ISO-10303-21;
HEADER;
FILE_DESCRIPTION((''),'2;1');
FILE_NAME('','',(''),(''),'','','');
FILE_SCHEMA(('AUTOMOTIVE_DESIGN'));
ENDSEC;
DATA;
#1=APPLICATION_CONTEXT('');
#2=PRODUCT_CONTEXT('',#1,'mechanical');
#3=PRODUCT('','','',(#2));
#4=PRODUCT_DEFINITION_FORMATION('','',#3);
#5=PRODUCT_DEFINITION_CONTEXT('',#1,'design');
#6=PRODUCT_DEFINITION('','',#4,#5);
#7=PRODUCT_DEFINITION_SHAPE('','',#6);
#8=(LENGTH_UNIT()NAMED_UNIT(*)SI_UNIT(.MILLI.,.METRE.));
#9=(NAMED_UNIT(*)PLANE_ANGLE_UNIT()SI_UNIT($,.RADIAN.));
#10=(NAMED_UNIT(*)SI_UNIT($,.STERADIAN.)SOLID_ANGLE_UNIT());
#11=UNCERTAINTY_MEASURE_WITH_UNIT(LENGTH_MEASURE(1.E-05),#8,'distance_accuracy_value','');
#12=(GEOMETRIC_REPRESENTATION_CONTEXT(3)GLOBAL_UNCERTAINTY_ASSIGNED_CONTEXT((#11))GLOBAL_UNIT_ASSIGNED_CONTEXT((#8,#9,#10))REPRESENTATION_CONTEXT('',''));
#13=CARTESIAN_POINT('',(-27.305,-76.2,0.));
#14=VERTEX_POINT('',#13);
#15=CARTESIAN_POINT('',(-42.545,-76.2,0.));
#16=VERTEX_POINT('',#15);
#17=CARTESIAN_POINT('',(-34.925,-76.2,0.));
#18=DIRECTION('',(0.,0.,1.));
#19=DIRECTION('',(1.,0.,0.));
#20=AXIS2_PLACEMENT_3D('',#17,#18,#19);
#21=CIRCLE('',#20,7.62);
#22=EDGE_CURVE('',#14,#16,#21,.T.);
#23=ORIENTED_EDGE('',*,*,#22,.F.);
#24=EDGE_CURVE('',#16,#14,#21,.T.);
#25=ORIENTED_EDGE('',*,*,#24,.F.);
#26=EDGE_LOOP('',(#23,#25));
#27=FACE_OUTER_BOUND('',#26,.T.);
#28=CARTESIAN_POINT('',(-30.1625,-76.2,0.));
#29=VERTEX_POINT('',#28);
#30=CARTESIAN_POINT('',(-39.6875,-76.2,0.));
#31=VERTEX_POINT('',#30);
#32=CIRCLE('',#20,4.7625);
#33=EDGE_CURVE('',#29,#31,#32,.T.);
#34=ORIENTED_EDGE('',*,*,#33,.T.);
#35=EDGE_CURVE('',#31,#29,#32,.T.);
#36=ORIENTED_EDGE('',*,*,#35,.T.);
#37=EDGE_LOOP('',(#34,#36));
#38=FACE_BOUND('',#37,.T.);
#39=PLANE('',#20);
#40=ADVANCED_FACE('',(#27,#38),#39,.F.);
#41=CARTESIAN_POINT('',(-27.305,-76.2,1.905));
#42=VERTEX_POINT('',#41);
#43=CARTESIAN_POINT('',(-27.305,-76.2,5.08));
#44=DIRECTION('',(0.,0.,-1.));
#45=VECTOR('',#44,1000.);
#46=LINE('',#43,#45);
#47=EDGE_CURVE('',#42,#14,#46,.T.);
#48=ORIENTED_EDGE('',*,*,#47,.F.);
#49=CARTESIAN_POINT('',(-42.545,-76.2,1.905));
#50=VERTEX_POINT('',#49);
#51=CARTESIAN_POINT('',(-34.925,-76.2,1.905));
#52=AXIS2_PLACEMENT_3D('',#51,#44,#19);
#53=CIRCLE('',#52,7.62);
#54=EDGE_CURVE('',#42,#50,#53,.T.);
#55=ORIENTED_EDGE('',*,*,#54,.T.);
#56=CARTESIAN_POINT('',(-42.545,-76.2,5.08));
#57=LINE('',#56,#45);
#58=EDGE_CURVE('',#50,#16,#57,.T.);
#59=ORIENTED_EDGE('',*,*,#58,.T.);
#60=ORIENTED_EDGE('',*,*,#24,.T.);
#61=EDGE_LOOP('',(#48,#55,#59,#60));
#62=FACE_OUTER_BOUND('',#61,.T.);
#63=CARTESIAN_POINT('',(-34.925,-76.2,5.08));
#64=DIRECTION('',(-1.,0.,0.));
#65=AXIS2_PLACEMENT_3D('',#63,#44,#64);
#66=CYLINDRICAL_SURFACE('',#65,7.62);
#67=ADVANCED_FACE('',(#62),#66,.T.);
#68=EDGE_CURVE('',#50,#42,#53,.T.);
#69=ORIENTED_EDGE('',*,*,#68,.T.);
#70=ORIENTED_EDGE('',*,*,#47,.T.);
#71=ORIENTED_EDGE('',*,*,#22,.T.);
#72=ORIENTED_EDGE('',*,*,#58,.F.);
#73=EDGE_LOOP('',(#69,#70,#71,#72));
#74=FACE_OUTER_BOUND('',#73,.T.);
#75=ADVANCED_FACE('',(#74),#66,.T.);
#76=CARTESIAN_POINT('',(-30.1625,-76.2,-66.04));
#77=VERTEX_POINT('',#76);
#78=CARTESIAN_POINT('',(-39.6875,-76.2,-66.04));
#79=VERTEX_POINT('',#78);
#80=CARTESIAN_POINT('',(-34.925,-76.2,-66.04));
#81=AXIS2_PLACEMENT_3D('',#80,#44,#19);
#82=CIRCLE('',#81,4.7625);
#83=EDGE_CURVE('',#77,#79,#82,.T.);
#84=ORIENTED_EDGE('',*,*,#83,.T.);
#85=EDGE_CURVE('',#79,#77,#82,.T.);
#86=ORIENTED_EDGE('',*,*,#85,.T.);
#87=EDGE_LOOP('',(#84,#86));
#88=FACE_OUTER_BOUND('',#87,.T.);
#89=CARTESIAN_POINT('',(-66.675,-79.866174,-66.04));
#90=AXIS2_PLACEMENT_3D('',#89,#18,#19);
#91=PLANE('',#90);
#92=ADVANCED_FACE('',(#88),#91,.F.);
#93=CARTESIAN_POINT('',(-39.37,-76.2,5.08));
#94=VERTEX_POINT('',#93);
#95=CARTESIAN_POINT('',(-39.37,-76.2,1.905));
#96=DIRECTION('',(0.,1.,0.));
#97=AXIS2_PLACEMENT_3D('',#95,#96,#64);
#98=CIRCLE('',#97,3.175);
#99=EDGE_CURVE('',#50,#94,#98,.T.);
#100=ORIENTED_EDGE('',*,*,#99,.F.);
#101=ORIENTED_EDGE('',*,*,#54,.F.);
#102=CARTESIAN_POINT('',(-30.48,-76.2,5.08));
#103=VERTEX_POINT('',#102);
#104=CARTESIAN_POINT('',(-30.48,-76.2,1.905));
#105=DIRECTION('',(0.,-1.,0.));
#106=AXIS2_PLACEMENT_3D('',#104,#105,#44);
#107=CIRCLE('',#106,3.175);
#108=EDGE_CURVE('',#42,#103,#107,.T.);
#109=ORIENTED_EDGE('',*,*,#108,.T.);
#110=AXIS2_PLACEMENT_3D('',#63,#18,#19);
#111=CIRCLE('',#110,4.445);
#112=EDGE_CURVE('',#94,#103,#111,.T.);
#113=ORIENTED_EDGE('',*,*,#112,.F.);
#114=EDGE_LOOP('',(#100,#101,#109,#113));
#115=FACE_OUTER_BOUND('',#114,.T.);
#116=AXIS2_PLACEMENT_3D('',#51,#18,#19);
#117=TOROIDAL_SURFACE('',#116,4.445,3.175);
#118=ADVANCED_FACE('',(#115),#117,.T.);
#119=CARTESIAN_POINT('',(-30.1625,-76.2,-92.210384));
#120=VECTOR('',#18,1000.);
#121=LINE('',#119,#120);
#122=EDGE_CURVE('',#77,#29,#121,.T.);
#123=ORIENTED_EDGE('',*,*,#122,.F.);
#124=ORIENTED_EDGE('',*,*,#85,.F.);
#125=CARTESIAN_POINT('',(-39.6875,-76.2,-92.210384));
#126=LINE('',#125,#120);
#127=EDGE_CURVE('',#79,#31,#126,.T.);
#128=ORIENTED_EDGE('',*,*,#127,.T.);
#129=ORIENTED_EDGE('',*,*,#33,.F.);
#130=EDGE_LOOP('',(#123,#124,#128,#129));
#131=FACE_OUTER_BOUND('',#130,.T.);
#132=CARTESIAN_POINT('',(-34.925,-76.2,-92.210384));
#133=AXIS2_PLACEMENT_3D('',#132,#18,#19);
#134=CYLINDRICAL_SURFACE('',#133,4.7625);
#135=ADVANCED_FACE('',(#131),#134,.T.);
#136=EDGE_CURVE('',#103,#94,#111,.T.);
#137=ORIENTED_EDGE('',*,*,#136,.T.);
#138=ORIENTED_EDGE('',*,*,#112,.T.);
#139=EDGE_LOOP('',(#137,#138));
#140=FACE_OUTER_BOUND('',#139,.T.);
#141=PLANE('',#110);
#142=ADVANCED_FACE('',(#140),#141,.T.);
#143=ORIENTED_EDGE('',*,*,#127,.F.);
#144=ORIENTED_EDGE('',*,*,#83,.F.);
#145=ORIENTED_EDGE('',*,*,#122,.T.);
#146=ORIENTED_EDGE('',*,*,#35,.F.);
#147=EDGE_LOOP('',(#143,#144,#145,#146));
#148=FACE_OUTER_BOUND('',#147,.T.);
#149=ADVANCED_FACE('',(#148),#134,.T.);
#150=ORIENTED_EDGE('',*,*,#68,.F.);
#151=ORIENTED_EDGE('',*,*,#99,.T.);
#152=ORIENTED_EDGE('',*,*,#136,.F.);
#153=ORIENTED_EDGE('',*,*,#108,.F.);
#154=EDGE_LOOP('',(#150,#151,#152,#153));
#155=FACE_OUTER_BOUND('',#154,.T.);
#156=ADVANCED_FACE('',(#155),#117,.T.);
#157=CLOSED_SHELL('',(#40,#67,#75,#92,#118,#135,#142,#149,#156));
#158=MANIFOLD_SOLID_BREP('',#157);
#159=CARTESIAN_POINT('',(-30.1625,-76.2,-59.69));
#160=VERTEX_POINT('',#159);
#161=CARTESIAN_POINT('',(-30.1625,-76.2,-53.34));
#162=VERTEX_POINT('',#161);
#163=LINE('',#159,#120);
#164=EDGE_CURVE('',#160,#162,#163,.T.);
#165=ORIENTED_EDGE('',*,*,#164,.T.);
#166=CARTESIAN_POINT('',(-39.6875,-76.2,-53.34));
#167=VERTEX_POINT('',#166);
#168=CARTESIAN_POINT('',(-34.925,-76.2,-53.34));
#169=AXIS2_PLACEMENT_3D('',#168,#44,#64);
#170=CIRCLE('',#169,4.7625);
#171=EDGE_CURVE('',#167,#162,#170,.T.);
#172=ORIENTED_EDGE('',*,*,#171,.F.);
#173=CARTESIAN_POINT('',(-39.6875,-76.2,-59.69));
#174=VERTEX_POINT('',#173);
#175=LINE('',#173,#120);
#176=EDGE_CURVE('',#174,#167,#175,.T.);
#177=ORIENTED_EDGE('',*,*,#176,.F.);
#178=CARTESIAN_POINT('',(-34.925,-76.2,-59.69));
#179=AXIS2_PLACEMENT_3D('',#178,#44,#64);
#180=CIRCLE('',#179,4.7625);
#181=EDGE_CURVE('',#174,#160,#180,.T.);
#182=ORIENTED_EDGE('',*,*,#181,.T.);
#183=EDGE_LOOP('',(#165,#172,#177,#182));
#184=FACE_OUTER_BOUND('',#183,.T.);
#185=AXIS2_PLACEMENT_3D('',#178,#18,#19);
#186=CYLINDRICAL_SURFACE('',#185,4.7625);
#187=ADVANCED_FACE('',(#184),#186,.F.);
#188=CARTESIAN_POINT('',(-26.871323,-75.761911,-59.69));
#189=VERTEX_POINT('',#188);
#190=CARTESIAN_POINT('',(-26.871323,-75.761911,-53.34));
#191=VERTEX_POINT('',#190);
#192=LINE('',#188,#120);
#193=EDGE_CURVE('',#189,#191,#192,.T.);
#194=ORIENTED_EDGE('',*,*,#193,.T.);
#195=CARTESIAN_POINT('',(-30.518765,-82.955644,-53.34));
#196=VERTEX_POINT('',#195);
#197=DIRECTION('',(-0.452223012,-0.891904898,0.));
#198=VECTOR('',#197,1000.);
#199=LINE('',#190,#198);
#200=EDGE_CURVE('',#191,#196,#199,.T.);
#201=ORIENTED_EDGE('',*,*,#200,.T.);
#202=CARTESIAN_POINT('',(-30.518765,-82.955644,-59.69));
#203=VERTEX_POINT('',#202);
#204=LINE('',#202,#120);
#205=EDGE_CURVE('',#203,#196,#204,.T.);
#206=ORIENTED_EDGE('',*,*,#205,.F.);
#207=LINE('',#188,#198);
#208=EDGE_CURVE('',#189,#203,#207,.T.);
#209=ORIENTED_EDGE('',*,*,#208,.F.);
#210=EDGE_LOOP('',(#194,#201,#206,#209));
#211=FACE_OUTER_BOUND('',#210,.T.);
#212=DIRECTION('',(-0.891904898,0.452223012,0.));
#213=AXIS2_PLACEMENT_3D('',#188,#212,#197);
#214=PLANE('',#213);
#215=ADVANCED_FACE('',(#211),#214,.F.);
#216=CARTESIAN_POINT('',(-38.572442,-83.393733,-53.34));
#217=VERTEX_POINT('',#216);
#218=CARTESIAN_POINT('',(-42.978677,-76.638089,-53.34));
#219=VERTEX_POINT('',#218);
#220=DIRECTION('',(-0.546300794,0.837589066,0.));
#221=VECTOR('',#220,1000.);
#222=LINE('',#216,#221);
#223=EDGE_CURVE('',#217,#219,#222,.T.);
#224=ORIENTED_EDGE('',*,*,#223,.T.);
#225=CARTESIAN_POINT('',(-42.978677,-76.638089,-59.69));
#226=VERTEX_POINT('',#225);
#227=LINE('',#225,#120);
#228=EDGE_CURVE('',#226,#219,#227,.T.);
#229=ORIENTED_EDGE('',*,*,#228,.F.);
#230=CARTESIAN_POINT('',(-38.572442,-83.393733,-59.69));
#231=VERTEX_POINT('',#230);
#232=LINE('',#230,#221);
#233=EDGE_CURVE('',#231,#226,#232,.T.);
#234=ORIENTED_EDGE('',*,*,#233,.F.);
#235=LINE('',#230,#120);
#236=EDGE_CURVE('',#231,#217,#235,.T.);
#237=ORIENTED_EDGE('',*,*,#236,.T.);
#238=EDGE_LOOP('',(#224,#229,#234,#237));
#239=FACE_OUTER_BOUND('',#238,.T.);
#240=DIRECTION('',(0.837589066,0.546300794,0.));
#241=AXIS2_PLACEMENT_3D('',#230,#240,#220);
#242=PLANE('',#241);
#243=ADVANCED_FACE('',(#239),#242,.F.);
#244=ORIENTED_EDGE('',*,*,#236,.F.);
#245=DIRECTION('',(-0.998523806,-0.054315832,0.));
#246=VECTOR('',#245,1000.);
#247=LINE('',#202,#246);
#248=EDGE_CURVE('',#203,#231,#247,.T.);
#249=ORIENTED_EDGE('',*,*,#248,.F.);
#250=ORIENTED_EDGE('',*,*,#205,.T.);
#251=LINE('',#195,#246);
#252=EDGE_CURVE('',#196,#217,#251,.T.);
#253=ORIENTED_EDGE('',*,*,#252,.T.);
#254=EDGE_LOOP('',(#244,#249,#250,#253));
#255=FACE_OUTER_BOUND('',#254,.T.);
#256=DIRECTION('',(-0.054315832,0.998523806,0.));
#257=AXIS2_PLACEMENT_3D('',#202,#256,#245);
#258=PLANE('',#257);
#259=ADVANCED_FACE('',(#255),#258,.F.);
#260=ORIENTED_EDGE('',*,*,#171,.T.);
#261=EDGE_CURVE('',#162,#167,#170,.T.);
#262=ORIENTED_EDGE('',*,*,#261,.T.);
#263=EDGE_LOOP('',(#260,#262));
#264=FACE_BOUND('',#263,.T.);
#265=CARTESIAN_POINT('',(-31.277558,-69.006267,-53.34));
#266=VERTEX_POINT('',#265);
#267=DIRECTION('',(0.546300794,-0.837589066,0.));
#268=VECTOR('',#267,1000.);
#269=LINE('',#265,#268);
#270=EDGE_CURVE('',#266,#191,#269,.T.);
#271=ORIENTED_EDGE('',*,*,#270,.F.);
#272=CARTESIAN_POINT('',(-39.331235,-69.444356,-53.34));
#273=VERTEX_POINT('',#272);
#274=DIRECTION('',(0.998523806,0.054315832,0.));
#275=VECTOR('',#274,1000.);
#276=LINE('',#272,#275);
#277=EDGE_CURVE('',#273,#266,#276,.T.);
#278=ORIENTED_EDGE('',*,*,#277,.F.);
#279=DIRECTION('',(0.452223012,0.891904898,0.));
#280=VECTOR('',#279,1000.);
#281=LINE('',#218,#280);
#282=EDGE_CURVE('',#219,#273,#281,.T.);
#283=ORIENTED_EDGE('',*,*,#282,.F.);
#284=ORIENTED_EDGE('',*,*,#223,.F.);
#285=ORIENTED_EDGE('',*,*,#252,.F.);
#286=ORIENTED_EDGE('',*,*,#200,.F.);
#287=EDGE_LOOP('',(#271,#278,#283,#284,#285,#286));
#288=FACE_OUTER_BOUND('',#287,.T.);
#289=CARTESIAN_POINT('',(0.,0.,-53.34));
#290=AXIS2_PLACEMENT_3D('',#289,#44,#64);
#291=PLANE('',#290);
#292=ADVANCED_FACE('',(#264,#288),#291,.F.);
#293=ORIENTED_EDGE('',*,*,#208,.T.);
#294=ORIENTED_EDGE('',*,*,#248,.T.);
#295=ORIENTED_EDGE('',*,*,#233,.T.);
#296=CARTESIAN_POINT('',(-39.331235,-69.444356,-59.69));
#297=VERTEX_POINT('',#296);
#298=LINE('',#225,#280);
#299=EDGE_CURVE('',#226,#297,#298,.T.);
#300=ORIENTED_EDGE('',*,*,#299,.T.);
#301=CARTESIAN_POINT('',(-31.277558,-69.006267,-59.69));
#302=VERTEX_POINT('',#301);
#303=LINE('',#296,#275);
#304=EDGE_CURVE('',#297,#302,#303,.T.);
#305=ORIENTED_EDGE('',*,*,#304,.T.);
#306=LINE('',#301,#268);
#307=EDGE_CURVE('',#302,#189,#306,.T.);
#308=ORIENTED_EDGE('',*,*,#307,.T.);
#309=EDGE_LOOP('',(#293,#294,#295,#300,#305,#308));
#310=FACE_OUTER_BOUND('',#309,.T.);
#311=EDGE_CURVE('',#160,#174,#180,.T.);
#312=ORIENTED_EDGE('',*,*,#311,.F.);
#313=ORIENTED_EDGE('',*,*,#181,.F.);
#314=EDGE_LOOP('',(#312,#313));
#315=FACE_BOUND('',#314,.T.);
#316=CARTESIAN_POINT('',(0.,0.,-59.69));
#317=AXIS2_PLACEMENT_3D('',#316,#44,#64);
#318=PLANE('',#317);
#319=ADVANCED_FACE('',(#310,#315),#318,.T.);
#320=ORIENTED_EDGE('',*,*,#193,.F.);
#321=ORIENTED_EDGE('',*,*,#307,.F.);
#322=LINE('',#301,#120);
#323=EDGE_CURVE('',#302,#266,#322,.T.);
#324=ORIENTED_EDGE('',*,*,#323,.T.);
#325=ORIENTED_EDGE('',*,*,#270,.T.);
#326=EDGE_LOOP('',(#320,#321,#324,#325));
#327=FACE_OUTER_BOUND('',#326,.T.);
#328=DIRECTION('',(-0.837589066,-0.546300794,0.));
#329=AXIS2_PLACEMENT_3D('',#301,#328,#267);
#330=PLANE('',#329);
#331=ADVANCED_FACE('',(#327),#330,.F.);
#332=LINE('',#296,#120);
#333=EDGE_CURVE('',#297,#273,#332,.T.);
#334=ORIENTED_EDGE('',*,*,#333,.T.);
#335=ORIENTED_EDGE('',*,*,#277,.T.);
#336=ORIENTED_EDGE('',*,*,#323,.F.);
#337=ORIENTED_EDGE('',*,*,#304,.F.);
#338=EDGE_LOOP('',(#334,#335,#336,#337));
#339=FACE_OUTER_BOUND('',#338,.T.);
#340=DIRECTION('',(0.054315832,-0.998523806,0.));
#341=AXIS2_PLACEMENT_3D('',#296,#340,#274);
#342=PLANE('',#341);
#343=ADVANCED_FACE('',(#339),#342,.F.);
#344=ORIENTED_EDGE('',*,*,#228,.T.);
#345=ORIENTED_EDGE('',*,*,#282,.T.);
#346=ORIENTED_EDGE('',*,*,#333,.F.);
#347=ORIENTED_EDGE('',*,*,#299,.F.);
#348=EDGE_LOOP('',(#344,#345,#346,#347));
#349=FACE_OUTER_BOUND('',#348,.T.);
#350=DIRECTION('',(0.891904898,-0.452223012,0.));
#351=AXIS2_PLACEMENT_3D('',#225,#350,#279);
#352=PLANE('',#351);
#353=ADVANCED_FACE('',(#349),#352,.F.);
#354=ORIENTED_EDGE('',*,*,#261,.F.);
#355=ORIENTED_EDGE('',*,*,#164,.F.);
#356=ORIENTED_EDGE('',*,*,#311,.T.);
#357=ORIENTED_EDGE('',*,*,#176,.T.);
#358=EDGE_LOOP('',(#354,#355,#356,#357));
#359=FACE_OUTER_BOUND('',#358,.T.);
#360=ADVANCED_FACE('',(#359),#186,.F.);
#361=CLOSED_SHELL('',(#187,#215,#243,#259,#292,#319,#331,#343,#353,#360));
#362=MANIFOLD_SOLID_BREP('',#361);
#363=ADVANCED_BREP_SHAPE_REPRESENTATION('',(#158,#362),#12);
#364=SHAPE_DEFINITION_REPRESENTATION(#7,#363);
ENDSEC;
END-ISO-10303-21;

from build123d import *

# Parameters (mm, degrees)
SKETCH1_R           = 4.7625
BOSS_EXTRUDE1_DEPTH = 66.04
SKETCH2_R           = 7.62
BOSS_EXTRUDE2_DEPTH = 5.08
FILLET1_R           = 3.175
SKETCH3_R           = 4.7625
BOSS_EXTRUDE3_DEPTH = 6.35


with BuildPart() as part:
    # Sketch1 → Boss-Extrude1 (new body)
    with BuildSketch(Plane.XY):
        with Locations((-34.925, -76.2)):
            Circle(SKETCH1_R)
    extrude(amount=-BOSS_EXTRUDE1_DEPTH)

    # Sketch2 → Boss-Extrude2 (add)
    with BuildSketch(Plane.XY):
        with Locations((-34.925, -76.2)):
            Circle(SKETCH2_R)
    extrude(amount=BOSS_EXTRUDE2_DEPTH)

    # Fillet1
    fillet1_edges = [part.edges().sort_by_distance(p)[0] for p in [
        (-42.545, -76.2, 5.08),
    ]]
    fillet(fillet1_edges, radius=FILLET1_R)


with BuildPart() as body_2:
    # Sketch3 → Boss-Extrude3 (new body)
    with BuildSketch(Plane(origin=(0, 0, -53.34), x_dir=(-1, 0, 0), z_dir=(0, 0, -1))):
        Polygon((39.331234536, -69.444355652), (31.277557644, -69.006266783), (26.871323108, -75.761911131), (30.518765464, -82.955644348), (38.572442356, -83.393733217), (42.978676892, -76.638088869), align=None)
        with Locations((34.925, -76.2)):
            Circle(SKETCH3_R, mode=Mode.SUBTRACT)
    extrude(amount=BOSS_EXTRUDE3_DEPTH)


solid = Compound([part.part, body_2.part])
